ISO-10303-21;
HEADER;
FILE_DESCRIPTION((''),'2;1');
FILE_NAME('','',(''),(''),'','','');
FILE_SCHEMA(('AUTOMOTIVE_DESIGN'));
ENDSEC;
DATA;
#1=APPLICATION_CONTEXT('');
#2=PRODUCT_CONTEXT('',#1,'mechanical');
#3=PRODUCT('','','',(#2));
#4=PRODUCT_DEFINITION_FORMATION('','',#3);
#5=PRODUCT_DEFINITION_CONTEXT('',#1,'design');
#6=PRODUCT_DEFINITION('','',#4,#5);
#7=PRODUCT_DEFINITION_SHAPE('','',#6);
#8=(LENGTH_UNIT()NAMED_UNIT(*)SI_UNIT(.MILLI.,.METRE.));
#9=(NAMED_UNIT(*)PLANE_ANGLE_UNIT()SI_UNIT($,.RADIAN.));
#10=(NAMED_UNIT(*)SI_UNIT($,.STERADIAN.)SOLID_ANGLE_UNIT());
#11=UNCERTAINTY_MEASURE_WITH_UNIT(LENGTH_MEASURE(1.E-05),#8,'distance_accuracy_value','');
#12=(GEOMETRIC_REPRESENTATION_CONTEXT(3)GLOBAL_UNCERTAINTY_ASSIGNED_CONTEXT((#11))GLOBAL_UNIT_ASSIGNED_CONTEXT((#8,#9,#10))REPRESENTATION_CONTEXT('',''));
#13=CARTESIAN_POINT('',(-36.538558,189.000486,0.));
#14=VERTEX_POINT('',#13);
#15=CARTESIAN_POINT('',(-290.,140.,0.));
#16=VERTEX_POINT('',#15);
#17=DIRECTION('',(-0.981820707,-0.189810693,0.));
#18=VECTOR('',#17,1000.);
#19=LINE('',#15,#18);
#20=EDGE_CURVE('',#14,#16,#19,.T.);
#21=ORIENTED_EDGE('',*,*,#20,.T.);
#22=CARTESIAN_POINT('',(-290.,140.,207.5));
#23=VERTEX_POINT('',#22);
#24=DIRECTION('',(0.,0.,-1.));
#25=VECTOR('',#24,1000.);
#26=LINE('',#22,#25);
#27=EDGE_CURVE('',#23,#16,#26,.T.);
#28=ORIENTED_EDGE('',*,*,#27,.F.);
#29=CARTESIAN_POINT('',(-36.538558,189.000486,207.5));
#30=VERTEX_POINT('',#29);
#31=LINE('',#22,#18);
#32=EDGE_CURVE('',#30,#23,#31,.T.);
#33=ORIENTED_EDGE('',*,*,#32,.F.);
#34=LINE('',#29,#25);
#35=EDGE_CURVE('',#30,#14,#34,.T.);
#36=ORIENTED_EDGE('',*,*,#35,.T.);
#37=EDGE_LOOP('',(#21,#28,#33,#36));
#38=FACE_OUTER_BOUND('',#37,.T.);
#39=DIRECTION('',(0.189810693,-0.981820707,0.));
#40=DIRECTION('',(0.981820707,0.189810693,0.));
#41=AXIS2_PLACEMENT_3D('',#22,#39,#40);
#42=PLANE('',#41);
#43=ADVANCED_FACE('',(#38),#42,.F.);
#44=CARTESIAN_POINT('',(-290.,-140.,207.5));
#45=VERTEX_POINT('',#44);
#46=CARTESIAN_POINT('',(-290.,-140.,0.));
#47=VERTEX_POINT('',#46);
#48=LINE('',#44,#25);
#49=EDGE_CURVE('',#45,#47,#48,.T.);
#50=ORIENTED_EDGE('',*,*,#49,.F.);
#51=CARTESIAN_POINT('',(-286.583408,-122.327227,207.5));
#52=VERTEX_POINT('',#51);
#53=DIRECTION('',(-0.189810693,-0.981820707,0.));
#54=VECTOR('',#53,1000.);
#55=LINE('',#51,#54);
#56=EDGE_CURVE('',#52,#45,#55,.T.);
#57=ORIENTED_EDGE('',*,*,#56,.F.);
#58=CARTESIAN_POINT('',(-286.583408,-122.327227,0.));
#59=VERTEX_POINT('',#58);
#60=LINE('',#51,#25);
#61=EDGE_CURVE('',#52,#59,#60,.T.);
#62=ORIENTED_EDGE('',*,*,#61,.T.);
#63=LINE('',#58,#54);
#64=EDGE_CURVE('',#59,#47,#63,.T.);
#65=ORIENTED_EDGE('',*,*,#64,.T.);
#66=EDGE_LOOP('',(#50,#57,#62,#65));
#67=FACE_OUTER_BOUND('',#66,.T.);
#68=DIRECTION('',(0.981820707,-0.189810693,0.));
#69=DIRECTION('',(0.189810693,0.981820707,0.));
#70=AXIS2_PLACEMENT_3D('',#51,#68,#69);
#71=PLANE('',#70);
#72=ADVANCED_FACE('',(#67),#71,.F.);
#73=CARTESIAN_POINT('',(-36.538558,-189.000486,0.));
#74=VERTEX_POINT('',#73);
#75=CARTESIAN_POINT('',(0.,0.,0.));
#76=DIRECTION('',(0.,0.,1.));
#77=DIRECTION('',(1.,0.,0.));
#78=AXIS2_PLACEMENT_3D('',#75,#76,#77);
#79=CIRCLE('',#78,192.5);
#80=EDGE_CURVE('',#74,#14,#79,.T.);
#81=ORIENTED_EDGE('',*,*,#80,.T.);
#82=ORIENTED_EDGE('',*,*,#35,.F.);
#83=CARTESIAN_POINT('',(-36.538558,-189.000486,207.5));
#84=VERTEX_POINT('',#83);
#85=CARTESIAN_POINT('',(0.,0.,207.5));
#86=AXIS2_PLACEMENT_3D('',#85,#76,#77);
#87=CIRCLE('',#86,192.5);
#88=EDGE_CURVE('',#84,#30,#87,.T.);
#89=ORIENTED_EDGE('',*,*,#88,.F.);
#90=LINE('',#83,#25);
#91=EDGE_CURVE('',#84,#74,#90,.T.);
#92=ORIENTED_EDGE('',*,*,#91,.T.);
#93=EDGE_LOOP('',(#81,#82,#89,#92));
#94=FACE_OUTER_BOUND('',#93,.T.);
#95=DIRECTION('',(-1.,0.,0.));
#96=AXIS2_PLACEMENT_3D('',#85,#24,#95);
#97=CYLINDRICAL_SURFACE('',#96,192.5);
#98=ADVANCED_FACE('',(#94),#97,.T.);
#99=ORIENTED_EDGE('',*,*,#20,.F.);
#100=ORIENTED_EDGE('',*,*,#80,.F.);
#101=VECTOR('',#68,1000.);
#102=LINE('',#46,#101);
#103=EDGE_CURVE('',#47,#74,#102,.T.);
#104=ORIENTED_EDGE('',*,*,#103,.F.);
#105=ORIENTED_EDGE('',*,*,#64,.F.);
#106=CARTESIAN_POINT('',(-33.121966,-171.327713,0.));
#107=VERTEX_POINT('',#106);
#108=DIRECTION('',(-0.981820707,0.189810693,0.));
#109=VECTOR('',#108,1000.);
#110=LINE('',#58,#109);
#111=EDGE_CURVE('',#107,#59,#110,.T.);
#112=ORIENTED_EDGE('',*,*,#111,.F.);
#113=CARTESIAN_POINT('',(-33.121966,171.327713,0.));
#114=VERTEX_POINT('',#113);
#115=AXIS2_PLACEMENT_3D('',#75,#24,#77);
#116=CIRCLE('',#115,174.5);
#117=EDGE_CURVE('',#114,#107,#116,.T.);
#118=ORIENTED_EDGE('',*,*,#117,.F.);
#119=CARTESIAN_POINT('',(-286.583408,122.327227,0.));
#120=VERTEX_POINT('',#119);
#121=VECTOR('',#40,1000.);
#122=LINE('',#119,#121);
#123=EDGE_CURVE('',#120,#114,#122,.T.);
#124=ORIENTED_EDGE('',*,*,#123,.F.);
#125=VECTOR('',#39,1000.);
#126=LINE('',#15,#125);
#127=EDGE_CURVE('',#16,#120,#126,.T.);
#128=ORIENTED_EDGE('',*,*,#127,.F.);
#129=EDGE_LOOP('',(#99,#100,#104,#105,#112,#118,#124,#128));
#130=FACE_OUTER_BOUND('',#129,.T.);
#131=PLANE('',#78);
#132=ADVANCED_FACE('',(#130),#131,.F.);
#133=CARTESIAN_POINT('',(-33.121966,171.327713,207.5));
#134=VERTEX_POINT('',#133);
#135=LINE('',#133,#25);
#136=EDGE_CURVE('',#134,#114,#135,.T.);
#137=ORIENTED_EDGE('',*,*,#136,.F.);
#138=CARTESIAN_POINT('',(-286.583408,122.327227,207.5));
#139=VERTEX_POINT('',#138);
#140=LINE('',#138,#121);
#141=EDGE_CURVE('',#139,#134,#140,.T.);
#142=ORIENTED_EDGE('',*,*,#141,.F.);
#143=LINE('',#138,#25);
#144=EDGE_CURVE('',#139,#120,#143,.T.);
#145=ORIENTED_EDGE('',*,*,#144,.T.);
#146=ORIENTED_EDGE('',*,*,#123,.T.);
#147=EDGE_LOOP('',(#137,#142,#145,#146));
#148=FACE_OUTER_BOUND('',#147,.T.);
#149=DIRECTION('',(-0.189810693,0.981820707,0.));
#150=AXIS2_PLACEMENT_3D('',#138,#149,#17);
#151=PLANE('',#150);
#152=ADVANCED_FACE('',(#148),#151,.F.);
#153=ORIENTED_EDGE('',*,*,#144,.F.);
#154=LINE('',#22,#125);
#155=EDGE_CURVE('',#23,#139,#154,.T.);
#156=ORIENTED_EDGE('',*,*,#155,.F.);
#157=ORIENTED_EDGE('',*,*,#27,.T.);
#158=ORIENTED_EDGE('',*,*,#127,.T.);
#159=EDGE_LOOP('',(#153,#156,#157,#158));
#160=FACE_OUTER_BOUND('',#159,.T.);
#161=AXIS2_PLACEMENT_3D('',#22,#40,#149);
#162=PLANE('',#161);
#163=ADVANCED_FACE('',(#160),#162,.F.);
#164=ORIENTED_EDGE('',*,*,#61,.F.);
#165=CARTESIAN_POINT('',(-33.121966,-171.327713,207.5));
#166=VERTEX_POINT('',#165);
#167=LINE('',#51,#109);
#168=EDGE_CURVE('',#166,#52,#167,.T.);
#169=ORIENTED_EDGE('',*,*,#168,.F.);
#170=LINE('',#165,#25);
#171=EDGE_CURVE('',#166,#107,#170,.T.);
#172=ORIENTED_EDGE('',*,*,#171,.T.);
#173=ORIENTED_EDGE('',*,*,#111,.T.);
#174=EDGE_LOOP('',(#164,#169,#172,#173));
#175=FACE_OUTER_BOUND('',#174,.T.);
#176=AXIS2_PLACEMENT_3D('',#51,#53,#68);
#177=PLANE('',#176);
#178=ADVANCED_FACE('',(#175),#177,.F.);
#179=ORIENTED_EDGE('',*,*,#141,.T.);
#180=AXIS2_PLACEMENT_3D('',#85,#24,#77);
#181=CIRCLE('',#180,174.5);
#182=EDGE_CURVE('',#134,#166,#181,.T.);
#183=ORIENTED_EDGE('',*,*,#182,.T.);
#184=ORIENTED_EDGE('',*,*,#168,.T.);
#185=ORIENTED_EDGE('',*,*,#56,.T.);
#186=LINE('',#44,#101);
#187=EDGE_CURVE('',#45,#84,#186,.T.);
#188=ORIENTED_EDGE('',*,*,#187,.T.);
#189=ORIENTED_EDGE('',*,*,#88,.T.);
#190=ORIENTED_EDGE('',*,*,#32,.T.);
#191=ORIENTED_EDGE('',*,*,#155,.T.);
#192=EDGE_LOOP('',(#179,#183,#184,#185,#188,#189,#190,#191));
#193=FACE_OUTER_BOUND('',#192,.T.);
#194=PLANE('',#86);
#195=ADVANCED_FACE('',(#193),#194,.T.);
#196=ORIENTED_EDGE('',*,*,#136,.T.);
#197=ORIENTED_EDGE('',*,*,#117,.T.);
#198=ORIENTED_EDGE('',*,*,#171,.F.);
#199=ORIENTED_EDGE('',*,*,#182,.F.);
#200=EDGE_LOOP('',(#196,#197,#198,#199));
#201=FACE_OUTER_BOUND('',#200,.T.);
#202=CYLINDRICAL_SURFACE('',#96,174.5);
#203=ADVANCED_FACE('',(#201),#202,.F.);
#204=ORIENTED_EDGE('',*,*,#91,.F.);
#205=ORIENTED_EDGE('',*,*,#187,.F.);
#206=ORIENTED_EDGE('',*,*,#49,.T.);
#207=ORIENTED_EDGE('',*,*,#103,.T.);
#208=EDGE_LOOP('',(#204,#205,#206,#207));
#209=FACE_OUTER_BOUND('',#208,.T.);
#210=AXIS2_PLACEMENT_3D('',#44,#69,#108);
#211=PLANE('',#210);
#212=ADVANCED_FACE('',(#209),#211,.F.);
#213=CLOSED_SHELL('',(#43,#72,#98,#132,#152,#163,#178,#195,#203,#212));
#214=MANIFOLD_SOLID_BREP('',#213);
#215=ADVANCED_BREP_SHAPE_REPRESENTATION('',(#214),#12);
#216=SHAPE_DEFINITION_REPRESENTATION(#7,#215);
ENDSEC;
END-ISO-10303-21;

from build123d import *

# Parameters (mm, degrees)
BOSS_EXTRUDE1_DEPTH = 207.5


with BuildPart() as part:
    # Sketch1 → Boss-Extrude1 (new body)
    with BuildSketch(Plane.XY):
        with BuildLine():
            Line((-290, 140), (-36.538558432, 189.000486104))
            ThreePointArc((-36.538558432, 189.000486104), (192.5, 0), (-36.538558432, -189.000486104))
            Line((-36.538558432, -189.000486104), (-290, -140))
            Line((-290, -140), (-286.583407523, -122.327227273))
            Line((-286.583407523, -122.327227273), (-33.121965956, -171.327713378))
            ThreePointArc((-33.121965956, -171.327713378), (174.5, 0), (-33.121965956, 171.327713378))
            Line((-33.121965956, 171.327713378), (-286.583407523, 122.327227273))
            Line((-286.583407523, 122.327227273), (-290, 140))
        make_face()
    extrude(amount=BOSS_EXTRUDE1_DEPTH)


solid = part.part
